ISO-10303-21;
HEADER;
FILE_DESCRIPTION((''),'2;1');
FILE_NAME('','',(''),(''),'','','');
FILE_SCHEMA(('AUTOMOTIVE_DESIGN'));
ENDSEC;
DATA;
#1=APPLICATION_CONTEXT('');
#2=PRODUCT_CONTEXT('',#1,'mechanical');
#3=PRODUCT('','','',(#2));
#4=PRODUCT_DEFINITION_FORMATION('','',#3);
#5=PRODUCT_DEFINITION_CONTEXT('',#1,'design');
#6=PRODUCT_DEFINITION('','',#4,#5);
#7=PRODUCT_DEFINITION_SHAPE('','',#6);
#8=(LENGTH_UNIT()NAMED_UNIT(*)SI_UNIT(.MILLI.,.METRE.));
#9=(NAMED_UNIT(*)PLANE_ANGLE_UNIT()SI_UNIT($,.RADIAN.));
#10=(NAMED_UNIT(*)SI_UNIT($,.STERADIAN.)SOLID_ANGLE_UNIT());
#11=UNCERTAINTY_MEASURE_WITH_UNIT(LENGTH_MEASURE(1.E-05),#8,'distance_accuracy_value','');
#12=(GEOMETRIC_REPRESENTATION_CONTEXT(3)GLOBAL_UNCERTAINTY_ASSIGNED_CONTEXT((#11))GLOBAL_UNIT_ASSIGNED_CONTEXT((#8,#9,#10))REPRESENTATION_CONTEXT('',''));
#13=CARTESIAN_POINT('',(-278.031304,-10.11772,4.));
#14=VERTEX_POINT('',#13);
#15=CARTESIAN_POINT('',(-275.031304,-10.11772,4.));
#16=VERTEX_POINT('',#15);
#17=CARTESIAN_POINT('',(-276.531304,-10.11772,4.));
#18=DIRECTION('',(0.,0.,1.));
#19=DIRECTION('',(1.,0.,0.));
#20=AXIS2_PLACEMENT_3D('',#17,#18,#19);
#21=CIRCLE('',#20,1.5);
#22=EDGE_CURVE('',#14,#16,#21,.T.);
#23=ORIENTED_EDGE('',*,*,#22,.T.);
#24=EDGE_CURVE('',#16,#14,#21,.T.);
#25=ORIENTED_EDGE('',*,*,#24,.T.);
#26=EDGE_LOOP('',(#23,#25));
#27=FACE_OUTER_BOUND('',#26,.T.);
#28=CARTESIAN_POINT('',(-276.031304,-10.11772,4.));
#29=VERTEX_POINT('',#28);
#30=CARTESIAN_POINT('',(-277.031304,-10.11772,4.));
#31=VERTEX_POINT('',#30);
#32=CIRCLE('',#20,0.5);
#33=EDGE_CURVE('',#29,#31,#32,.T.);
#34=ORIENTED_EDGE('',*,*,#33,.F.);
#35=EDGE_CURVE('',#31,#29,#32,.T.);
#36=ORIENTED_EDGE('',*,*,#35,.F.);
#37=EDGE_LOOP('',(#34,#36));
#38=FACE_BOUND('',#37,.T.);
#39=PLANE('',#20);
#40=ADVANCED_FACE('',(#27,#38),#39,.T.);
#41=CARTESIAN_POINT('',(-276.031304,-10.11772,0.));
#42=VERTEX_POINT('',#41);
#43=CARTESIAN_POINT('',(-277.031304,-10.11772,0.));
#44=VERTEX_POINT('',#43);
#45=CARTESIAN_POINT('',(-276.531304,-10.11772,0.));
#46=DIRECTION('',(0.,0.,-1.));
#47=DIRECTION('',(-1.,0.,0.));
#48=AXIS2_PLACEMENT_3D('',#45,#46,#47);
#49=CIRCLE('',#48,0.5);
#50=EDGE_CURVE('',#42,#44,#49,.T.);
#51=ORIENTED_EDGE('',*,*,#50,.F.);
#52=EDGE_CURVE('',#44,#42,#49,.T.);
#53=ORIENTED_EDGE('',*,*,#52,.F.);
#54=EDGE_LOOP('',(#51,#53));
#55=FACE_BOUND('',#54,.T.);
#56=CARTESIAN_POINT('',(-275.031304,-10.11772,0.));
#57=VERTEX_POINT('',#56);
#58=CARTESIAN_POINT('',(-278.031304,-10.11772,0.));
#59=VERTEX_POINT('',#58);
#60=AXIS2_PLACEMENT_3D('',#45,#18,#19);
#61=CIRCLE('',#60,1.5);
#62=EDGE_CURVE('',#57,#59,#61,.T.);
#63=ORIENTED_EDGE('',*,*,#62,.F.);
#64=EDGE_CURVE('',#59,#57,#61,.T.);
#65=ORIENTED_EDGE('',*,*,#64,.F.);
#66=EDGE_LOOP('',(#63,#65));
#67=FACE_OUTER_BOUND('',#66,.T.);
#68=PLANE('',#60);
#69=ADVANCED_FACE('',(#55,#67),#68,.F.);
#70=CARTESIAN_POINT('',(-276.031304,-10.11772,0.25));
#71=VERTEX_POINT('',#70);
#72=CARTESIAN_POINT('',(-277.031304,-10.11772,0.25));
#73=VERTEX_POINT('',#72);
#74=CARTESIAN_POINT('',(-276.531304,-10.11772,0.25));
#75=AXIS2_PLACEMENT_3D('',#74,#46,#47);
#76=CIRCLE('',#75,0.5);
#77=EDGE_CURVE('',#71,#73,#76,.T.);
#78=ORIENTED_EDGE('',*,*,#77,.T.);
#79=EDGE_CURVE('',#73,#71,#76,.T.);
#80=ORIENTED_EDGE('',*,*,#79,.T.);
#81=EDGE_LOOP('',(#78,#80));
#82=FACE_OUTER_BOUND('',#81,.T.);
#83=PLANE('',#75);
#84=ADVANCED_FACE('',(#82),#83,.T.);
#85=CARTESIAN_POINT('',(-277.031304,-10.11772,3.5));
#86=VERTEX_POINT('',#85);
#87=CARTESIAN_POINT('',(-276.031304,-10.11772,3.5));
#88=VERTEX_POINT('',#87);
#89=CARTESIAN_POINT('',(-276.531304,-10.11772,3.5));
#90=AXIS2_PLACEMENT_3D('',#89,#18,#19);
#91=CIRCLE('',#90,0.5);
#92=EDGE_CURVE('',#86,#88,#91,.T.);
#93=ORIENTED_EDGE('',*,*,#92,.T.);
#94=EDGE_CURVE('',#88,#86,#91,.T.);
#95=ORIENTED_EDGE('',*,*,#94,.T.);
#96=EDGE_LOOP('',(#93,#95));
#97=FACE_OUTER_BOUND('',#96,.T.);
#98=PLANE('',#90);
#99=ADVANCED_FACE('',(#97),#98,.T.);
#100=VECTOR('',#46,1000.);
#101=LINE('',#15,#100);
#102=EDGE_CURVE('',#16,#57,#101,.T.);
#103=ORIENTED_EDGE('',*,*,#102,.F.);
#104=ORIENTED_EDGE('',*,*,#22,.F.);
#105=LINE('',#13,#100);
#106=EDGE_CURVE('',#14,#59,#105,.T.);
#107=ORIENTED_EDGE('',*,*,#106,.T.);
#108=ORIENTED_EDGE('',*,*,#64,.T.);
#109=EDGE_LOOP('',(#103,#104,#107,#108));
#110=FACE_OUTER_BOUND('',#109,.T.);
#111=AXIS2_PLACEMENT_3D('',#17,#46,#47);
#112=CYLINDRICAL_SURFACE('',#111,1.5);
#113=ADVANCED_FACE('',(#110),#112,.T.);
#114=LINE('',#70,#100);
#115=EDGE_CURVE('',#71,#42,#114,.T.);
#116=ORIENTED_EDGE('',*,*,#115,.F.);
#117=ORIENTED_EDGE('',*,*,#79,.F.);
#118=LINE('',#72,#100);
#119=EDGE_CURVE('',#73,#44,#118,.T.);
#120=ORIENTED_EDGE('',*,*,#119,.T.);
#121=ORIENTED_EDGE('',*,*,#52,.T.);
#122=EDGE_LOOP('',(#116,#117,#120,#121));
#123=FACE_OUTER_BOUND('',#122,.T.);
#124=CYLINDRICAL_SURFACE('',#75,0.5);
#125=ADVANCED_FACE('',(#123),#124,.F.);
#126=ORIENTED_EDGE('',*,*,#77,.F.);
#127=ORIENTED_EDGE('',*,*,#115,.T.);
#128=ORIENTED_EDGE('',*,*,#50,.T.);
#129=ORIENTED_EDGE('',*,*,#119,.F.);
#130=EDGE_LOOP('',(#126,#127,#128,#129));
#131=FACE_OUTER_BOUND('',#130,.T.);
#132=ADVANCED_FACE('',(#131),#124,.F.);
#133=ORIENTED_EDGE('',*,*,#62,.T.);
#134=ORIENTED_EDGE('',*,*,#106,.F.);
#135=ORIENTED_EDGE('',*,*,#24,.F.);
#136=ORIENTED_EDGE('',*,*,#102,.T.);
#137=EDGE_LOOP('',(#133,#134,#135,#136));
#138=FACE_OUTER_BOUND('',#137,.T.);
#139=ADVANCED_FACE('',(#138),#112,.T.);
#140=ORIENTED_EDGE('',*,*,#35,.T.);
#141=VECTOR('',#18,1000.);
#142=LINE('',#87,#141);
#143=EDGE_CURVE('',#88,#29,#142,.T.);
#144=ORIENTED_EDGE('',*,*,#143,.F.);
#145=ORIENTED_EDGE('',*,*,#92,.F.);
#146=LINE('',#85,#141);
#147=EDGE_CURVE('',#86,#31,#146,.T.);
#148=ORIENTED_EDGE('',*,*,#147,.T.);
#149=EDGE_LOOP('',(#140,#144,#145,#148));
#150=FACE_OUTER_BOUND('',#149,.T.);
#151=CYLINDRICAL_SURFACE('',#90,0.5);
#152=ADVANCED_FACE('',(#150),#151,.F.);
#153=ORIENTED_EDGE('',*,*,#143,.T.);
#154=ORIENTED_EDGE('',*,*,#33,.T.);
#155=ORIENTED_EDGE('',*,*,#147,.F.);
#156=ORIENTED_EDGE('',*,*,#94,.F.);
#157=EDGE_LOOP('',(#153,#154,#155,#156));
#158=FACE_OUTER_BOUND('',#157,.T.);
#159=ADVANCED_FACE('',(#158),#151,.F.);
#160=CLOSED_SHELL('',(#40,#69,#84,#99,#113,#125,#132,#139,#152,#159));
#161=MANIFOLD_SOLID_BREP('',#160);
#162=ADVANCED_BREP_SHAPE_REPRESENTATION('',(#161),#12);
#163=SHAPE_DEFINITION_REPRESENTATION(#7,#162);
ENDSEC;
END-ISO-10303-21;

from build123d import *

# Parameters (mm, degrees)
SKETCH1_R           = 1.5
BOSS_EXTRUDE1_DEPTH = 4
SKETCH4_R           = 0.5
CUT_EXTRUDE1_DEPTH  = 0.5
CUT_EXTRUDE2_START  = -0.25
SKETCH5_R           = 0.5
CUT_EXTRUDE2_DEPTH  = 0.25


with BuildPart() as part:
    # Sketch1 → Boss-Extrude1 (new body)
    with BuildSketch(Plane.XY):
        with Locations((-276.531304302, -10.117720272)):
            Circle(SKETCH1_R)
    extrude(amount=BOSS_EXTRUDE1_DEPTH)

    # Sketch4 → Cut-Extrude1 (cut)
    with BuildSketch(Plane.XY.offset(4)):
        with Locations((-276.531304302, -10.117720272)):
            Circle(SKETCH4_R)
    extrude(amount=-CUT_EXTRUDE1_DEPTH, mode=Mode.SUBTRACT)

    # Sketch5 → Cut-Extrude2 (cut)
    with BuildSketch(Plane(origin=(0, 0, 0), x_dir=(-1, 0, 0), z_dir=(0, 0, -1)).offset(CUT_EXTRUDE2_START)):
        with Locations(Location((276.531304302, -10.117720272, 0), (0, 0, 180))):
            Circle(SKETCH5_R)
    extrude(amount=CUT_EXTRUDE2_DEPTH, mode=Mode.SUBTRACT)


solid = part.part
